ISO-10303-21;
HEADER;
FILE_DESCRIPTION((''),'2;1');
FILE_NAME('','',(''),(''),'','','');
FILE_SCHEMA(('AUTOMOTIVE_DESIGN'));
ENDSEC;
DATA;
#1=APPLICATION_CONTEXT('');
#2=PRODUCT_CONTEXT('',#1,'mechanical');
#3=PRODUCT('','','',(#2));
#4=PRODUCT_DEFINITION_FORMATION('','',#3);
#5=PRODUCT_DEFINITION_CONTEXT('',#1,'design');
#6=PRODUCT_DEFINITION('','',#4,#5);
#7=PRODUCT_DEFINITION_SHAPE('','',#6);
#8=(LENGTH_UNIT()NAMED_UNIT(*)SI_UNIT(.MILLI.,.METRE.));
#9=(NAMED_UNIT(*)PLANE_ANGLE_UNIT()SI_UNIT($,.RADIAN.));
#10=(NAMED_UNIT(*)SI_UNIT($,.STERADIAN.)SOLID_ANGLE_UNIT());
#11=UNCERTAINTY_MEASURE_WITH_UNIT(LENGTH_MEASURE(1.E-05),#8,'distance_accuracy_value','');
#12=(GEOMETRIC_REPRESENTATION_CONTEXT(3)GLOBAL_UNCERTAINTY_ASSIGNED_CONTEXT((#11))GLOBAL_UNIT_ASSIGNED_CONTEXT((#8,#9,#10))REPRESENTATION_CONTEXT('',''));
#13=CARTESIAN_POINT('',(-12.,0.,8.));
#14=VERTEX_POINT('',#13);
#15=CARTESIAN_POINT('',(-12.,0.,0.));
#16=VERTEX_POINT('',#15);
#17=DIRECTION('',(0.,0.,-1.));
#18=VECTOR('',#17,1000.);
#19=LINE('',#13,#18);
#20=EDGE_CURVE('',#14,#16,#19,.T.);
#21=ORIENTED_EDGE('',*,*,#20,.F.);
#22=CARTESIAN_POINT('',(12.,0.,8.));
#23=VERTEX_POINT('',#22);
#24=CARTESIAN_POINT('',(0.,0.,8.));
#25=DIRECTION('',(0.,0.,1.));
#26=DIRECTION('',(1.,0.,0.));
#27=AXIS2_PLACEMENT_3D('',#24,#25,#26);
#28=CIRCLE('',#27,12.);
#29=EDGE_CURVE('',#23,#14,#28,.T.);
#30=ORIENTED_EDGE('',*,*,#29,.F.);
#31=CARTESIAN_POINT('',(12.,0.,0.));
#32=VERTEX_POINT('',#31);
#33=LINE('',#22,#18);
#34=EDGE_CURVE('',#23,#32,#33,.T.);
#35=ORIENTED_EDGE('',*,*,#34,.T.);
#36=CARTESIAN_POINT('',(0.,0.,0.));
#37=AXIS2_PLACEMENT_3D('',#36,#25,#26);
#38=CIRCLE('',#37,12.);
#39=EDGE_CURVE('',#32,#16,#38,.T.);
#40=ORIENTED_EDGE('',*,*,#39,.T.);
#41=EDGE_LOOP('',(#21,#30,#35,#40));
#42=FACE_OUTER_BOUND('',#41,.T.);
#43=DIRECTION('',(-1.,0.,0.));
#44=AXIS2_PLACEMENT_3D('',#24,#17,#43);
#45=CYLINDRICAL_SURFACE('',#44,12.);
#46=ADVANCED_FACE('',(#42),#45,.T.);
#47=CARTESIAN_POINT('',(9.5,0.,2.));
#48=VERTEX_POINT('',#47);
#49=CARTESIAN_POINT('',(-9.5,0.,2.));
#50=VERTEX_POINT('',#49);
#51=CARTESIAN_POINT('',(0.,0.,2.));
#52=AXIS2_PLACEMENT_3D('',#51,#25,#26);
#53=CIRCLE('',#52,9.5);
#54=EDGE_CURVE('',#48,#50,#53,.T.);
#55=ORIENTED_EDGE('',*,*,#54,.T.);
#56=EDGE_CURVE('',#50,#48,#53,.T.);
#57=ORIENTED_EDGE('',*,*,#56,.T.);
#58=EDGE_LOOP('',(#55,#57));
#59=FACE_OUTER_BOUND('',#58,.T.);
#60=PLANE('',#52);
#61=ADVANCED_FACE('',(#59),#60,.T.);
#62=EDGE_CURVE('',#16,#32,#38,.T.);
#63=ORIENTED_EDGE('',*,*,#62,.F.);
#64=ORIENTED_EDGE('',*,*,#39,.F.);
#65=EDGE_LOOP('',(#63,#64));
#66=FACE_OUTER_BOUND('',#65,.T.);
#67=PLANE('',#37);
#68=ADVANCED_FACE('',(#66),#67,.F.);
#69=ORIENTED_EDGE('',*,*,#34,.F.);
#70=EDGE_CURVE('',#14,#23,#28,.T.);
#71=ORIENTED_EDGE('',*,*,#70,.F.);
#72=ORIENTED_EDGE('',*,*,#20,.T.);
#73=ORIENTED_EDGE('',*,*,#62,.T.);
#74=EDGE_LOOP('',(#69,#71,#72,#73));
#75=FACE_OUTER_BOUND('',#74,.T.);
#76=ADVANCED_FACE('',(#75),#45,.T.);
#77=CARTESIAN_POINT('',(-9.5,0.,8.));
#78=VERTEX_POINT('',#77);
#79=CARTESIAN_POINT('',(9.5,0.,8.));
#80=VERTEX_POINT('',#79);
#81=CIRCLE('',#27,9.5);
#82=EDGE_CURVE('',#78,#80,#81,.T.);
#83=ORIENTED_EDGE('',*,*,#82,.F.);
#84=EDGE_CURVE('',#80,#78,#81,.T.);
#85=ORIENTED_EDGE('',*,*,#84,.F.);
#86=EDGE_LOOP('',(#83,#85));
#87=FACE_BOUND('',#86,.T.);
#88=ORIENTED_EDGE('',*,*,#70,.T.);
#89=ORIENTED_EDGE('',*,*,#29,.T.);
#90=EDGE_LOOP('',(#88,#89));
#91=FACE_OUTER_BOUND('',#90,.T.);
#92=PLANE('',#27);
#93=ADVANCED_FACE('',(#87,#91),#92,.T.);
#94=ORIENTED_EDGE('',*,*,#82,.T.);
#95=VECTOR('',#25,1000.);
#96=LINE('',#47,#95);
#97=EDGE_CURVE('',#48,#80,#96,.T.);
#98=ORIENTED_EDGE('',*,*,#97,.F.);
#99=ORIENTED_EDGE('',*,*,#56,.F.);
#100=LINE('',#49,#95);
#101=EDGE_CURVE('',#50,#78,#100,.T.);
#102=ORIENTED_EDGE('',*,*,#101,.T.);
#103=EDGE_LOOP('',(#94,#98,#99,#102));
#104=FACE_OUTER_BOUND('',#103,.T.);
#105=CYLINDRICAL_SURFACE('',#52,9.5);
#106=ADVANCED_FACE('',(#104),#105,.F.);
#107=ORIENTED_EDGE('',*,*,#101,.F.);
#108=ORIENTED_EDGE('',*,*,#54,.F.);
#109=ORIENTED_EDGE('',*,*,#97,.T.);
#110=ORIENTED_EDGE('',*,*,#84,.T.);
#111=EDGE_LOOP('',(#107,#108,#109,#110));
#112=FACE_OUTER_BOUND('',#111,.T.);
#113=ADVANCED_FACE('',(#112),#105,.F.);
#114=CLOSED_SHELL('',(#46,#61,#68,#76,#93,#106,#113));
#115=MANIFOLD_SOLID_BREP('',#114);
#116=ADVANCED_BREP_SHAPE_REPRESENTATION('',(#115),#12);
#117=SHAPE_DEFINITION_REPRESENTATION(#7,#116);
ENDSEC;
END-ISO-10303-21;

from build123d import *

# Parameters (mm, degrees)
SKETCH1_R           = 12
BOSS_EXTRUDE1_DEPTH = 8
SKETCH2_R           = 9.5
CUT_EXTRUDE1_DEPTH  = 6


with BuildPart() as part:
    # Sketch1 → Boss-Extrude1 (new body)
    with BuildSketch(Plane.XY):
        Circle(SKETCH1_R)
    extrude(amount=BOSS_EXTRUDE1_DEPTH)

    # Sketch2 → Cut-Extrude1 (cut)
    with BuildSketch(Plane.XY.offset(8)):
        Circle(SKETCH2_R)
    extrude(amount=-CUT_EXTRUDE1_DEPTH, mode=Mode.SUBTRACT)


solid = part.part
